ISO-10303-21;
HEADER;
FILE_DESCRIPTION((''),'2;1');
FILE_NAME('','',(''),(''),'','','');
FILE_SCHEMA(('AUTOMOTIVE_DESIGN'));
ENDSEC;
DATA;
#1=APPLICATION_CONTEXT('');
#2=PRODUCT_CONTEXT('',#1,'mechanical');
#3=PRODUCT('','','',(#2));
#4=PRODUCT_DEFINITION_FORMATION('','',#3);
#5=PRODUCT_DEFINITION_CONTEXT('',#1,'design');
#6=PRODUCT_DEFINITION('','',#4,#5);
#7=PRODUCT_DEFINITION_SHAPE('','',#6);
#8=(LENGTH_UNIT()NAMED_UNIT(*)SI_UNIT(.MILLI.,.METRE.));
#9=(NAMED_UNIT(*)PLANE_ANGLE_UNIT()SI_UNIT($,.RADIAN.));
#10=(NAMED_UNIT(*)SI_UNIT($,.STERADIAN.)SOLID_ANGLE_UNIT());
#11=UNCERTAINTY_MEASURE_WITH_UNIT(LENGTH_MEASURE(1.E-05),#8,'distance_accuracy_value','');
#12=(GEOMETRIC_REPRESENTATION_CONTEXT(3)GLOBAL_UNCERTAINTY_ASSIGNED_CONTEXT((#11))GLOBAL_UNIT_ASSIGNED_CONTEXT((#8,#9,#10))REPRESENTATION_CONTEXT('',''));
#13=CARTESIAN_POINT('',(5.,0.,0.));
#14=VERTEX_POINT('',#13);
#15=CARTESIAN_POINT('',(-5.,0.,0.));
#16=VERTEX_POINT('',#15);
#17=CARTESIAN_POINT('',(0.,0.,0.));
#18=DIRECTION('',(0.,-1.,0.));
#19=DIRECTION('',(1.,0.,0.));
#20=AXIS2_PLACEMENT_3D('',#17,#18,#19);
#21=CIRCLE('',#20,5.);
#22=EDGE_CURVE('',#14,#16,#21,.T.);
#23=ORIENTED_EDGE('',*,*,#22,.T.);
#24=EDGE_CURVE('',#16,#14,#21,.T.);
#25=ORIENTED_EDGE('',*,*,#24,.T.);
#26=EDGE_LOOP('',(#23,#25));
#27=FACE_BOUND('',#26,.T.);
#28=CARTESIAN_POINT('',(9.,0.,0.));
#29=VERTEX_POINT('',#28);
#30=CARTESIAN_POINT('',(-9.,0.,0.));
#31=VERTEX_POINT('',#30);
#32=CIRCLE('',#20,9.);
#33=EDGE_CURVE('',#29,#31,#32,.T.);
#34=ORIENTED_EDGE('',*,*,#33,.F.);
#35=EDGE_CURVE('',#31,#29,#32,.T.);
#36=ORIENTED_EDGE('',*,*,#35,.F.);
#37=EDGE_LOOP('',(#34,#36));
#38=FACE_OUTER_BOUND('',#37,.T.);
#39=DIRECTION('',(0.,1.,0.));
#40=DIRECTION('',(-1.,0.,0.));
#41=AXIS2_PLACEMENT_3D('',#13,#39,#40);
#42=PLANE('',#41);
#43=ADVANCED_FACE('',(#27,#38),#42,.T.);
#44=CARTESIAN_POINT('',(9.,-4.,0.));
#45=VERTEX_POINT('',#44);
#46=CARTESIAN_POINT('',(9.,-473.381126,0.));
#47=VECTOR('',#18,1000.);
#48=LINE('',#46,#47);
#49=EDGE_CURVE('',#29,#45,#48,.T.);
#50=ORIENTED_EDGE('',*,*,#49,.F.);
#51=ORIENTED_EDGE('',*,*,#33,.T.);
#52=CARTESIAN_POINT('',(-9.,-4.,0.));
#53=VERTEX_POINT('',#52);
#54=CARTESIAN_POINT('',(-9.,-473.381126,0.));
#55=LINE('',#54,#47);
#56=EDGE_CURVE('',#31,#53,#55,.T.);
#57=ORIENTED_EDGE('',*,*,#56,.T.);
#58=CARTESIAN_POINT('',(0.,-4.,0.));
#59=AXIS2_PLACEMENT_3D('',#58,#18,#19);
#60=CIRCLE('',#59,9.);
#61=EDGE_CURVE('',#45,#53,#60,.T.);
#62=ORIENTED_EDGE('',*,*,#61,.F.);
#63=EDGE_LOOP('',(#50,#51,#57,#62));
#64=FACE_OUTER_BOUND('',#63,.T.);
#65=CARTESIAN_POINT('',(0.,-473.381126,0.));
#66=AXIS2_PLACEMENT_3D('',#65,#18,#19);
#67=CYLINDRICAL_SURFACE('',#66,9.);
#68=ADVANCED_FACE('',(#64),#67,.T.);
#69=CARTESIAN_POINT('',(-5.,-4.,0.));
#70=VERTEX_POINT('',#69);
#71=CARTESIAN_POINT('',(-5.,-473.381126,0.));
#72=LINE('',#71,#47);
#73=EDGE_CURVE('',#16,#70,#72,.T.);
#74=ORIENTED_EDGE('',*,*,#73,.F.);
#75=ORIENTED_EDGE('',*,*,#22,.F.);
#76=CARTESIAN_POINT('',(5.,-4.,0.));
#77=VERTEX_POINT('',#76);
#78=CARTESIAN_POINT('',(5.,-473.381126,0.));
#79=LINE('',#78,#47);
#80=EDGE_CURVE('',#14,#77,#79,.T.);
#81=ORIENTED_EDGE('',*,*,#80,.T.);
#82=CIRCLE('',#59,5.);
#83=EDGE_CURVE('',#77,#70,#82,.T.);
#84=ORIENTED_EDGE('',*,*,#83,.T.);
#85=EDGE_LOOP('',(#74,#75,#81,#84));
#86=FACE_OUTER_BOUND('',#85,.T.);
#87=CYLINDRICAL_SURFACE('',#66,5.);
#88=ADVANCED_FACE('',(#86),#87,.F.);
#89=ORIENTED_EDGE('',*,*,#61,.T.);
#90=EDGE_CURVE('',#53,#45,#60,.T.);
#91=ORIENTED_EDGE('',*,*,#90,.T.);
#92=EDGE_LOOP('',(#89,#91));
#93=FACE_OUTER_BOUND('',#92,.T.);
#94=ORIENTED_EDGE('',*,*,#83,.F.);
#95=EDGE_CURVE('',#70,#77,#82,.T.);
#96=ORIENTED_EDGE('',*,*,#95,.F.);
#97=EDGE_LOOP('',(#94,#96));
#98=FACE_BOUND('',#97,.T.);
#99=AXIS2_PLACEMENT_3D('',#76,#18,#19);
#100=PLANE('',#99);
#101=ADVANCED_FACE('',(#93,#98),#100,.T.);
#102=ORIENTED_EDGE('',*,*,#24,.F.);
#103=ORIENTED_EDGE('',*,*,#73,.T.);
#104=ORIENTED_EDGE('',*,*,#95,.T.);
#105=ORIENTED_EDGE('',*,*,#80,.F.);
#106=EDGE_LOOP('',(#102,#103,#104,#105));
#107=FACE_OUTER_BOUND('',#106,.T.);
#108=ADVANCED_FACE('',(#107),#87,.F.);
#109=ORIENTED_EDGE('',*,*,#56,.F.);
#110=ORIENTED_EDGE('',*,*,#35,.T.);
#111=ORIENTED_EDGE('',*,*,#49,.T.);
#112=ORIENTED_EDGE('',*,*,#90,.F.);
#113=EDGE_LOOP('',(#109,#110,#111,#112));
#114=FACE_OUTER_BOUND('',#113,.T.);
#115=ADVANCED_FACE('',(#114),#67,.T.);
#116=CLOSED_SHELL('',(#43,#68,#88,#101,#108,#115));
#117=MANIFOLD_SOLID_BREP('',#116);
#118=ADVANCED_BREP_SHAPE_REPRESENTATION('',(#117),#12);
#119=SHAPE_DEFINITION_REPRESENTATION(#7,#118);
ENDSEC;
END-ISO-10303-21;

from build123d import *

# Parameters (mm, degrees)
SKETCH1_W = 4
SKETCH1_H = 4


with BuildPart() as part:
    # Sketch1 → Revolve1 (revolve)
    with BuildSketch(Plane.XY):
        with Locations((7, -2)):
            Rectangle(SKETCH1_W, SKETCH1_H)
    revolve(axis=Axis((0, -473.381125867, 0), (0, 1, 0)))


solid = part.part
